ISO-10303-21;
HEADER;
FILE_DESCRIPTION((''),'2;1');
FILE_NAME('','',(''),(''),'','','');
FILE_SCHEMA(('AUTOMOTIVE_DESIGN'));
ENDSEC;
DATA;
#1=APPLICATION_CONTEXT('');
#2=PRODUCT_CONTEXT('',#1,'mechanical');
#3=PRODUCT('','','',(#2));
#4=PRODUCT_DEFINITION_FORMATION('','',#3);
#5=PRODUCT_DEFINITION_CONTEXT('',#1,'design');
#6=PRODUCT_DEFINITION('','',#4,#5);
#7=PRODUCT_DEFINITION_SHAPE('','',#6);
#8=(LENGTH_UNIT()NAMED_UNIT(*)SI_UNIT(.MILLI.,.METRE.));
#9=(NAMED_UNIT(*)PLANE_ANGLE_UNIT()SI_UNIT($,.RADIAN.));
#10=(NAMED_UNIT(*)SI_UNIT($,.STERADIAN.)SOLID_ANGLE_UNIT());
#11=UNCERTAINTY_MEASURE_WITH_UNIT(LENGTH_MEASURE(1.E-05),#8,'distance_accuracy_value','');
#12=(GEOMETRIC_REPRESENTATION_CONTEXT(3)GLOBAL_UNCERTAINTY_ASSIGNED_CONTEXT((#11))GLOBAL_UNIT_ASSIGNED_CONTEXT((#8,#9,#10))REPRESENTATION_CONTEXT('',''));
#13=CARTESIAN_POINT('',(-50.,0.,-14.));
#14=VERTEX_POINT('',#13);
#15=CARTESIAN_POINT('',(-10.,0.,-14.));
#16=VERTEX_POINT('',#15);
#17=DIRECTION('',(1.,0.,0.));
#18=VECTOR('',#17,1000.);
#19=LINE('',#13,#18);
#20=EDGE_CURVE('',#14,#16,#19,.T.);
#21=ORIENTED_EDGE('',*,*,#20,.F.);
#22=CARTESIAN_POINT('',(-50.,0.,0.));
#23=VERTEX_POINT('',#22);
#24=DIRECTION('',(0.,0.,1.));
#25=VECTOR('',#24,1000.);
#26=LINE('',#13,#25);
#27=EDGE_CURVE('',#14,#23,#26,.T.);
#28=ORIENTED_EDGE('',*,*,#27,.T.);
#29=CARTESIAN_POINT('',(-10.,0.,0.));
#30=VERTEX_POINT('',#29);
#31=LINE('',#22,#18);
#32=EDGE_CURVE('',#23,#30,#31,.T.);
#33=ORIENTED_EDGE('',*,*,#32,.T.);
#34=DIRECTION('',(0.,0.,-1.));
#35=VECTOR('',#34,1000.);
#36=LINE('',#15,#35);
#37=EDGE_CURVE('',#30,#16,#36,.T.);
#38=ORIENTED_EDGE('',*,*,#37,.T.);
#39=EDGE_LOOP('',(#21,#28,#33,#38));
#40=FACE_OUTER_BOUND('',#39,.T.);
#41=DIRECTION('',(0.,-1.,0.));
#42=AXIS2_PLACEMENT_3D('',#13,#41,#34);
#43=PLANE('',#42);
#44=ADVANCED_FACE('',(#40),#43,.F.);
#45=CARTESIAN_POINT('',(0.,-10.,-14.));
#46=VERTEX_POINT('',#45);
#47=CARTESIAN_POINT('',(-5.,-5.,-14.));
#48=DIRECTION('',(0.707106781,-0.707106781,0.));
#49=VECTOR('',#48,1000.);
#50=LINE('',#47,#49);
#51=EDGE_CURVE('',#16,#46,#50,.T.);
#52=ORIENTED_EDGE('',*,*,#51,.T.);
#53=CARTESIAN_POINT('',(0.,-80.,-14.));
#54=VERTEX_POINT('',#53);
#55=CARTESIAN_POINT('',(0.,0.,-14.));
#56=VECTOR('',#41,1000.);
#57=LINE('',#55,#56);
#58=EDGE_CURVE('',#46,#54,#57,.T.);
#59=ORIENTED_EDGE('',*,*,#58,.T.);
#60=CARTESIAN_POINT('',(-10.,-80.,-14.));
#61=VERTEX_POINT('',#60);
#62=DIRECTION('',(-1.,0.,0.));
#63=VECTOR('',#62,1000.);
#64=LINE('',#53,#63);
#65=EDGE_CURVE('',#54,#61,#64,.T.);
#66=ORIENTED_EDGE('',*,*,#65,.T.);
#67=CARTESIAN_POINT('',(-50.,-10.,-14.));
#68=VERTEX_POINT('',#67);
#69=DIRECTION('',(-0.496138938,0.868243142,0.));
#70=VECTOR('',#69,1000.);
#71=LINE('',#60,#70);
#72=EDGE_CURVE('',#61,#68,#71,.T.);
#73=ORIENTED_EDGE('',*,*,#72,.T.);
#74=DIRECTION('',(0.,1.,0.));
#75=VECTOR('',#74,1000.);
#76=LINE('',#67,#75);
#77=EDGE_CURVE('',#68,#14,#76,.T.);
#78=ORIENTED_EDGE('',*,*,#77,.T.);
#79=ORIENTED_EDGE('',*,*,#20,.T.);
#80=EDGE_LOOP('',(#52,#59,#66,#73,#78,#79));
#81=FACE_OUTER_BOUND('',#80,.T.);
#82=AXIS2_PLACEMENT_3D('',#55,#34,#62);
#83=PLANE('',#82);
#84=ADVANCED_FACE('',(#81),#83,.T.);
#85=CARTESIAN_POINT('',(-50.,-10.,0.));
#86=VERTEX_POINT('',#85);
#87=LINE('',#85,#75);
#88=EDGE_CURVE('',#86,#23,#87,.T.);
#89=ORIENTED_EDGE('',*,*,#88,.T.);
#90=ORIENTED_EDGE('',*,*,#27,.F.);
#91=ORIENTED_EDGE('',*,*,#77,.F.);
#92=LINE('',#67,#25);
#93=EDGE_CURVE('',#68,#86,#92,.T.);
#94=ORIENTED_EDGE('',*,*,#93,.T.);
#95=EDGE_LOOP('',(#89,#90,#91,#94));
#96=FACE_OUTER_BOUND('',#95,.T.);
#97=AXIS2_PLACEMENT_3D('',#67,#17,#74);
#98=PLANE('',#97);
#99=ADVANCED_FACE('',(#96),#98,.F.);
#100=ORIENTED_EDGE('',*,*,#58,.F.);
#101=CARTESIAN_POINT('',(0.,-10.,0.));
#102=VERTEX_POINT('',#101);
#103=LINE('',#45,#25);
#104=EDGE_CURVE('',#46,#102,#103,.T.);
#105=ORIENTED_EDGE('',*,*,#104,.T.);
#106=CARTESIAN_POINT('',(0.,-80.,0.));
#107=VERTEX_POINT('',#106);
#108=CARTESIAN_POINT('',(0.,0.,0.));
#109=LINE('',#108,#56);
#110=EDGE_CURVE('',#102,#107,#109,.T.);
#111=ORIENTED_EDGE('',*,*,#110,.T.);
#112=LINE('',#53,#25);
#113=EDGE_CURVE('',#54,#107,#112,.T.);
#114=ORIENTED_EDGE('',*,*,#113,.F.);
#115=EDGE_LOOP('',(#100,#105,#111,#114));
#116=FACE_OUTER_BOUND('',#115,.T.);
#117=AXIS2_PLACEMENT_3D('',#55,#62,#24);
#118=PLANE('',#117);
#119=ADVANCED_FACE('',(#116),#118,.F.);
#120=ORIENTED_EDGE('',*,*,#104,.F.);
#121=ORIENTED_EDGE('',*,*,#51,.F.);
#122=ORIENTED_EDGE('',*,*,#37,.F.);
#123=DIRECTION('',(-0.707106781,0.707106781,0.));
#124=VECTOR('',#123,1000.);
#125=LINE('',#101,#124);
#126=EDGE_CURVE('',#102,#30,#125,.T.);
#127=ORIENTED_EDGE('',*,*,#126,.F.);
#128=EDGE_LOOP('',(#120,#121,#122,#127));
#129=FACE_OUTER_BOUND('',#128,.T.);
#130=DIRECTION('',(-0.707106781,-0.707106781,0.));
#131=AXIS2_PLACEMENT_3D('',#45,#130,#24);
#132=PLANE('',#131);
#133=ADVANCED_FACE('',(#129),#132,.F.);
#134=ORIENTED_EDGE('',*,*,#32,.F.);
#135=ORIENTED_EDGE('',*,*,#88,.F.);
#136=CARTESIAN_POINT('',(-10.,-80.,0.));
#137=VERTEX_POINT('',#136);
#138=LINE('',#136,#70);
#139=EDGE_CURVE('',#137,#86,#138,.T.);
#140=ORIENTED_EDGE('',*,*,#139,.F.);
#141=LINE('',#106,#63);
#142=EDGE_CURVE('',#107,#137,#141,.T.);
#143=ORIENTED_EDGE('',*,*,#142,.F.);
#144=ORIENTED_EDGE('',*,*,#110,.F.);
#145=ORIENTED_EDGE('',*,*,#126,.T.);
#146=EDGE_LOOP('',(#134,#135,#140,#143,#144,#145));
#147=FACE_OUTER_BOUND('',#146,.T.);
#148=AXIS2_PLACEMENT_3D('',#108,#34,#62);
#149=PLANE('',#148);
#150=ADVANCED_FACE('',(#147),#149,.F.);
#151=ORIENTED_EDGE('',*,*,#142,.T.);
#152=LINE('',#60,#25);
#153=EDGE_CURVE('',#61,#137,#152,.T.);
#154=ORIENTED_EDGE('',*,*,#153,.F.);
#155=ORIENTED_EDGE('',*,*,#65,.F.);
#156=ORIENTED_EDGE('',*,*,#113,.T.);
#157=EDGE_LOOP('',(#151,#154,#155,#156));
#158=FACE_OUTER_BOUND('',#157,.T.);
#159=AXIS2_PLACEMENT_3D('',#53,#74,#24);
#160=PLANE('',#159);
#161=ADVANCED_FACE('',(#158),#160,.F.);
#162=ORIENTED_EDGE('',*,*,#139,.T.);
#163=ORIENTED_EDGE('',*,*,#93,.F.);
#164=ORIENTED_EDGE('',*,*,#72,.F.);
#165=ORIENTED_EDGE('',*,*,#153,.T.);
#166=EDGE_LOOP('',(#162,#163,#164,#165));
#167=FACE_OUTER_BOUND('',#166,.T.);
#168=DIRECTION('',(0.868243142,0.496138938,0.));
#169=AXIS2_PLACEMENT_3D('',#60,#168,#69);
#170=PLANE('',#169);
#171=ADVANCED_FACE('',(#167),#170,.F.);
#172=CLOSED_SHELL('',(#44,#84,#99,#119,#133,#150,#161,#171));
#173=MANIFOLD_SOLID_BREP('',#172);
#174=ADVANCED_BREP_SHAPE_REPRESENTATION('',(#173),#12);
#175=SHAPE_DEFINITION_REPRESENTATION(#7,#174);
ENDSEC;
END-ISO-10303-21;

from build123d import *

# Parameters (mm, degrees)
BOSS_EXTRUDE1_DEPTH = 14
CHAMFER1_SIZE       = 10


with BuildPart() as part:
    # Sketch1 → Boss-Extrude1 (new body)
    with BuildSketch(Plane(origin=(0, 0, 0), x_dir=(1, 0, 0), z_dir=(0, 0, -1))):
        Polygon((0, 0), (0, 80), (-10, 80), (-50, 10), (-50, 0), align=None)
    extrude(amount=BOSS_EXTRUDE1_DEPTH)

    # Chamfer1
    chamfer1_edges = [part.edges().sort_by_distance(p)[0] for p in [
        (0, 0, -7),
    ]]
    chamfer(chamfer1_edges, length=CHAMFER1_SIZE)


solid = part.part
